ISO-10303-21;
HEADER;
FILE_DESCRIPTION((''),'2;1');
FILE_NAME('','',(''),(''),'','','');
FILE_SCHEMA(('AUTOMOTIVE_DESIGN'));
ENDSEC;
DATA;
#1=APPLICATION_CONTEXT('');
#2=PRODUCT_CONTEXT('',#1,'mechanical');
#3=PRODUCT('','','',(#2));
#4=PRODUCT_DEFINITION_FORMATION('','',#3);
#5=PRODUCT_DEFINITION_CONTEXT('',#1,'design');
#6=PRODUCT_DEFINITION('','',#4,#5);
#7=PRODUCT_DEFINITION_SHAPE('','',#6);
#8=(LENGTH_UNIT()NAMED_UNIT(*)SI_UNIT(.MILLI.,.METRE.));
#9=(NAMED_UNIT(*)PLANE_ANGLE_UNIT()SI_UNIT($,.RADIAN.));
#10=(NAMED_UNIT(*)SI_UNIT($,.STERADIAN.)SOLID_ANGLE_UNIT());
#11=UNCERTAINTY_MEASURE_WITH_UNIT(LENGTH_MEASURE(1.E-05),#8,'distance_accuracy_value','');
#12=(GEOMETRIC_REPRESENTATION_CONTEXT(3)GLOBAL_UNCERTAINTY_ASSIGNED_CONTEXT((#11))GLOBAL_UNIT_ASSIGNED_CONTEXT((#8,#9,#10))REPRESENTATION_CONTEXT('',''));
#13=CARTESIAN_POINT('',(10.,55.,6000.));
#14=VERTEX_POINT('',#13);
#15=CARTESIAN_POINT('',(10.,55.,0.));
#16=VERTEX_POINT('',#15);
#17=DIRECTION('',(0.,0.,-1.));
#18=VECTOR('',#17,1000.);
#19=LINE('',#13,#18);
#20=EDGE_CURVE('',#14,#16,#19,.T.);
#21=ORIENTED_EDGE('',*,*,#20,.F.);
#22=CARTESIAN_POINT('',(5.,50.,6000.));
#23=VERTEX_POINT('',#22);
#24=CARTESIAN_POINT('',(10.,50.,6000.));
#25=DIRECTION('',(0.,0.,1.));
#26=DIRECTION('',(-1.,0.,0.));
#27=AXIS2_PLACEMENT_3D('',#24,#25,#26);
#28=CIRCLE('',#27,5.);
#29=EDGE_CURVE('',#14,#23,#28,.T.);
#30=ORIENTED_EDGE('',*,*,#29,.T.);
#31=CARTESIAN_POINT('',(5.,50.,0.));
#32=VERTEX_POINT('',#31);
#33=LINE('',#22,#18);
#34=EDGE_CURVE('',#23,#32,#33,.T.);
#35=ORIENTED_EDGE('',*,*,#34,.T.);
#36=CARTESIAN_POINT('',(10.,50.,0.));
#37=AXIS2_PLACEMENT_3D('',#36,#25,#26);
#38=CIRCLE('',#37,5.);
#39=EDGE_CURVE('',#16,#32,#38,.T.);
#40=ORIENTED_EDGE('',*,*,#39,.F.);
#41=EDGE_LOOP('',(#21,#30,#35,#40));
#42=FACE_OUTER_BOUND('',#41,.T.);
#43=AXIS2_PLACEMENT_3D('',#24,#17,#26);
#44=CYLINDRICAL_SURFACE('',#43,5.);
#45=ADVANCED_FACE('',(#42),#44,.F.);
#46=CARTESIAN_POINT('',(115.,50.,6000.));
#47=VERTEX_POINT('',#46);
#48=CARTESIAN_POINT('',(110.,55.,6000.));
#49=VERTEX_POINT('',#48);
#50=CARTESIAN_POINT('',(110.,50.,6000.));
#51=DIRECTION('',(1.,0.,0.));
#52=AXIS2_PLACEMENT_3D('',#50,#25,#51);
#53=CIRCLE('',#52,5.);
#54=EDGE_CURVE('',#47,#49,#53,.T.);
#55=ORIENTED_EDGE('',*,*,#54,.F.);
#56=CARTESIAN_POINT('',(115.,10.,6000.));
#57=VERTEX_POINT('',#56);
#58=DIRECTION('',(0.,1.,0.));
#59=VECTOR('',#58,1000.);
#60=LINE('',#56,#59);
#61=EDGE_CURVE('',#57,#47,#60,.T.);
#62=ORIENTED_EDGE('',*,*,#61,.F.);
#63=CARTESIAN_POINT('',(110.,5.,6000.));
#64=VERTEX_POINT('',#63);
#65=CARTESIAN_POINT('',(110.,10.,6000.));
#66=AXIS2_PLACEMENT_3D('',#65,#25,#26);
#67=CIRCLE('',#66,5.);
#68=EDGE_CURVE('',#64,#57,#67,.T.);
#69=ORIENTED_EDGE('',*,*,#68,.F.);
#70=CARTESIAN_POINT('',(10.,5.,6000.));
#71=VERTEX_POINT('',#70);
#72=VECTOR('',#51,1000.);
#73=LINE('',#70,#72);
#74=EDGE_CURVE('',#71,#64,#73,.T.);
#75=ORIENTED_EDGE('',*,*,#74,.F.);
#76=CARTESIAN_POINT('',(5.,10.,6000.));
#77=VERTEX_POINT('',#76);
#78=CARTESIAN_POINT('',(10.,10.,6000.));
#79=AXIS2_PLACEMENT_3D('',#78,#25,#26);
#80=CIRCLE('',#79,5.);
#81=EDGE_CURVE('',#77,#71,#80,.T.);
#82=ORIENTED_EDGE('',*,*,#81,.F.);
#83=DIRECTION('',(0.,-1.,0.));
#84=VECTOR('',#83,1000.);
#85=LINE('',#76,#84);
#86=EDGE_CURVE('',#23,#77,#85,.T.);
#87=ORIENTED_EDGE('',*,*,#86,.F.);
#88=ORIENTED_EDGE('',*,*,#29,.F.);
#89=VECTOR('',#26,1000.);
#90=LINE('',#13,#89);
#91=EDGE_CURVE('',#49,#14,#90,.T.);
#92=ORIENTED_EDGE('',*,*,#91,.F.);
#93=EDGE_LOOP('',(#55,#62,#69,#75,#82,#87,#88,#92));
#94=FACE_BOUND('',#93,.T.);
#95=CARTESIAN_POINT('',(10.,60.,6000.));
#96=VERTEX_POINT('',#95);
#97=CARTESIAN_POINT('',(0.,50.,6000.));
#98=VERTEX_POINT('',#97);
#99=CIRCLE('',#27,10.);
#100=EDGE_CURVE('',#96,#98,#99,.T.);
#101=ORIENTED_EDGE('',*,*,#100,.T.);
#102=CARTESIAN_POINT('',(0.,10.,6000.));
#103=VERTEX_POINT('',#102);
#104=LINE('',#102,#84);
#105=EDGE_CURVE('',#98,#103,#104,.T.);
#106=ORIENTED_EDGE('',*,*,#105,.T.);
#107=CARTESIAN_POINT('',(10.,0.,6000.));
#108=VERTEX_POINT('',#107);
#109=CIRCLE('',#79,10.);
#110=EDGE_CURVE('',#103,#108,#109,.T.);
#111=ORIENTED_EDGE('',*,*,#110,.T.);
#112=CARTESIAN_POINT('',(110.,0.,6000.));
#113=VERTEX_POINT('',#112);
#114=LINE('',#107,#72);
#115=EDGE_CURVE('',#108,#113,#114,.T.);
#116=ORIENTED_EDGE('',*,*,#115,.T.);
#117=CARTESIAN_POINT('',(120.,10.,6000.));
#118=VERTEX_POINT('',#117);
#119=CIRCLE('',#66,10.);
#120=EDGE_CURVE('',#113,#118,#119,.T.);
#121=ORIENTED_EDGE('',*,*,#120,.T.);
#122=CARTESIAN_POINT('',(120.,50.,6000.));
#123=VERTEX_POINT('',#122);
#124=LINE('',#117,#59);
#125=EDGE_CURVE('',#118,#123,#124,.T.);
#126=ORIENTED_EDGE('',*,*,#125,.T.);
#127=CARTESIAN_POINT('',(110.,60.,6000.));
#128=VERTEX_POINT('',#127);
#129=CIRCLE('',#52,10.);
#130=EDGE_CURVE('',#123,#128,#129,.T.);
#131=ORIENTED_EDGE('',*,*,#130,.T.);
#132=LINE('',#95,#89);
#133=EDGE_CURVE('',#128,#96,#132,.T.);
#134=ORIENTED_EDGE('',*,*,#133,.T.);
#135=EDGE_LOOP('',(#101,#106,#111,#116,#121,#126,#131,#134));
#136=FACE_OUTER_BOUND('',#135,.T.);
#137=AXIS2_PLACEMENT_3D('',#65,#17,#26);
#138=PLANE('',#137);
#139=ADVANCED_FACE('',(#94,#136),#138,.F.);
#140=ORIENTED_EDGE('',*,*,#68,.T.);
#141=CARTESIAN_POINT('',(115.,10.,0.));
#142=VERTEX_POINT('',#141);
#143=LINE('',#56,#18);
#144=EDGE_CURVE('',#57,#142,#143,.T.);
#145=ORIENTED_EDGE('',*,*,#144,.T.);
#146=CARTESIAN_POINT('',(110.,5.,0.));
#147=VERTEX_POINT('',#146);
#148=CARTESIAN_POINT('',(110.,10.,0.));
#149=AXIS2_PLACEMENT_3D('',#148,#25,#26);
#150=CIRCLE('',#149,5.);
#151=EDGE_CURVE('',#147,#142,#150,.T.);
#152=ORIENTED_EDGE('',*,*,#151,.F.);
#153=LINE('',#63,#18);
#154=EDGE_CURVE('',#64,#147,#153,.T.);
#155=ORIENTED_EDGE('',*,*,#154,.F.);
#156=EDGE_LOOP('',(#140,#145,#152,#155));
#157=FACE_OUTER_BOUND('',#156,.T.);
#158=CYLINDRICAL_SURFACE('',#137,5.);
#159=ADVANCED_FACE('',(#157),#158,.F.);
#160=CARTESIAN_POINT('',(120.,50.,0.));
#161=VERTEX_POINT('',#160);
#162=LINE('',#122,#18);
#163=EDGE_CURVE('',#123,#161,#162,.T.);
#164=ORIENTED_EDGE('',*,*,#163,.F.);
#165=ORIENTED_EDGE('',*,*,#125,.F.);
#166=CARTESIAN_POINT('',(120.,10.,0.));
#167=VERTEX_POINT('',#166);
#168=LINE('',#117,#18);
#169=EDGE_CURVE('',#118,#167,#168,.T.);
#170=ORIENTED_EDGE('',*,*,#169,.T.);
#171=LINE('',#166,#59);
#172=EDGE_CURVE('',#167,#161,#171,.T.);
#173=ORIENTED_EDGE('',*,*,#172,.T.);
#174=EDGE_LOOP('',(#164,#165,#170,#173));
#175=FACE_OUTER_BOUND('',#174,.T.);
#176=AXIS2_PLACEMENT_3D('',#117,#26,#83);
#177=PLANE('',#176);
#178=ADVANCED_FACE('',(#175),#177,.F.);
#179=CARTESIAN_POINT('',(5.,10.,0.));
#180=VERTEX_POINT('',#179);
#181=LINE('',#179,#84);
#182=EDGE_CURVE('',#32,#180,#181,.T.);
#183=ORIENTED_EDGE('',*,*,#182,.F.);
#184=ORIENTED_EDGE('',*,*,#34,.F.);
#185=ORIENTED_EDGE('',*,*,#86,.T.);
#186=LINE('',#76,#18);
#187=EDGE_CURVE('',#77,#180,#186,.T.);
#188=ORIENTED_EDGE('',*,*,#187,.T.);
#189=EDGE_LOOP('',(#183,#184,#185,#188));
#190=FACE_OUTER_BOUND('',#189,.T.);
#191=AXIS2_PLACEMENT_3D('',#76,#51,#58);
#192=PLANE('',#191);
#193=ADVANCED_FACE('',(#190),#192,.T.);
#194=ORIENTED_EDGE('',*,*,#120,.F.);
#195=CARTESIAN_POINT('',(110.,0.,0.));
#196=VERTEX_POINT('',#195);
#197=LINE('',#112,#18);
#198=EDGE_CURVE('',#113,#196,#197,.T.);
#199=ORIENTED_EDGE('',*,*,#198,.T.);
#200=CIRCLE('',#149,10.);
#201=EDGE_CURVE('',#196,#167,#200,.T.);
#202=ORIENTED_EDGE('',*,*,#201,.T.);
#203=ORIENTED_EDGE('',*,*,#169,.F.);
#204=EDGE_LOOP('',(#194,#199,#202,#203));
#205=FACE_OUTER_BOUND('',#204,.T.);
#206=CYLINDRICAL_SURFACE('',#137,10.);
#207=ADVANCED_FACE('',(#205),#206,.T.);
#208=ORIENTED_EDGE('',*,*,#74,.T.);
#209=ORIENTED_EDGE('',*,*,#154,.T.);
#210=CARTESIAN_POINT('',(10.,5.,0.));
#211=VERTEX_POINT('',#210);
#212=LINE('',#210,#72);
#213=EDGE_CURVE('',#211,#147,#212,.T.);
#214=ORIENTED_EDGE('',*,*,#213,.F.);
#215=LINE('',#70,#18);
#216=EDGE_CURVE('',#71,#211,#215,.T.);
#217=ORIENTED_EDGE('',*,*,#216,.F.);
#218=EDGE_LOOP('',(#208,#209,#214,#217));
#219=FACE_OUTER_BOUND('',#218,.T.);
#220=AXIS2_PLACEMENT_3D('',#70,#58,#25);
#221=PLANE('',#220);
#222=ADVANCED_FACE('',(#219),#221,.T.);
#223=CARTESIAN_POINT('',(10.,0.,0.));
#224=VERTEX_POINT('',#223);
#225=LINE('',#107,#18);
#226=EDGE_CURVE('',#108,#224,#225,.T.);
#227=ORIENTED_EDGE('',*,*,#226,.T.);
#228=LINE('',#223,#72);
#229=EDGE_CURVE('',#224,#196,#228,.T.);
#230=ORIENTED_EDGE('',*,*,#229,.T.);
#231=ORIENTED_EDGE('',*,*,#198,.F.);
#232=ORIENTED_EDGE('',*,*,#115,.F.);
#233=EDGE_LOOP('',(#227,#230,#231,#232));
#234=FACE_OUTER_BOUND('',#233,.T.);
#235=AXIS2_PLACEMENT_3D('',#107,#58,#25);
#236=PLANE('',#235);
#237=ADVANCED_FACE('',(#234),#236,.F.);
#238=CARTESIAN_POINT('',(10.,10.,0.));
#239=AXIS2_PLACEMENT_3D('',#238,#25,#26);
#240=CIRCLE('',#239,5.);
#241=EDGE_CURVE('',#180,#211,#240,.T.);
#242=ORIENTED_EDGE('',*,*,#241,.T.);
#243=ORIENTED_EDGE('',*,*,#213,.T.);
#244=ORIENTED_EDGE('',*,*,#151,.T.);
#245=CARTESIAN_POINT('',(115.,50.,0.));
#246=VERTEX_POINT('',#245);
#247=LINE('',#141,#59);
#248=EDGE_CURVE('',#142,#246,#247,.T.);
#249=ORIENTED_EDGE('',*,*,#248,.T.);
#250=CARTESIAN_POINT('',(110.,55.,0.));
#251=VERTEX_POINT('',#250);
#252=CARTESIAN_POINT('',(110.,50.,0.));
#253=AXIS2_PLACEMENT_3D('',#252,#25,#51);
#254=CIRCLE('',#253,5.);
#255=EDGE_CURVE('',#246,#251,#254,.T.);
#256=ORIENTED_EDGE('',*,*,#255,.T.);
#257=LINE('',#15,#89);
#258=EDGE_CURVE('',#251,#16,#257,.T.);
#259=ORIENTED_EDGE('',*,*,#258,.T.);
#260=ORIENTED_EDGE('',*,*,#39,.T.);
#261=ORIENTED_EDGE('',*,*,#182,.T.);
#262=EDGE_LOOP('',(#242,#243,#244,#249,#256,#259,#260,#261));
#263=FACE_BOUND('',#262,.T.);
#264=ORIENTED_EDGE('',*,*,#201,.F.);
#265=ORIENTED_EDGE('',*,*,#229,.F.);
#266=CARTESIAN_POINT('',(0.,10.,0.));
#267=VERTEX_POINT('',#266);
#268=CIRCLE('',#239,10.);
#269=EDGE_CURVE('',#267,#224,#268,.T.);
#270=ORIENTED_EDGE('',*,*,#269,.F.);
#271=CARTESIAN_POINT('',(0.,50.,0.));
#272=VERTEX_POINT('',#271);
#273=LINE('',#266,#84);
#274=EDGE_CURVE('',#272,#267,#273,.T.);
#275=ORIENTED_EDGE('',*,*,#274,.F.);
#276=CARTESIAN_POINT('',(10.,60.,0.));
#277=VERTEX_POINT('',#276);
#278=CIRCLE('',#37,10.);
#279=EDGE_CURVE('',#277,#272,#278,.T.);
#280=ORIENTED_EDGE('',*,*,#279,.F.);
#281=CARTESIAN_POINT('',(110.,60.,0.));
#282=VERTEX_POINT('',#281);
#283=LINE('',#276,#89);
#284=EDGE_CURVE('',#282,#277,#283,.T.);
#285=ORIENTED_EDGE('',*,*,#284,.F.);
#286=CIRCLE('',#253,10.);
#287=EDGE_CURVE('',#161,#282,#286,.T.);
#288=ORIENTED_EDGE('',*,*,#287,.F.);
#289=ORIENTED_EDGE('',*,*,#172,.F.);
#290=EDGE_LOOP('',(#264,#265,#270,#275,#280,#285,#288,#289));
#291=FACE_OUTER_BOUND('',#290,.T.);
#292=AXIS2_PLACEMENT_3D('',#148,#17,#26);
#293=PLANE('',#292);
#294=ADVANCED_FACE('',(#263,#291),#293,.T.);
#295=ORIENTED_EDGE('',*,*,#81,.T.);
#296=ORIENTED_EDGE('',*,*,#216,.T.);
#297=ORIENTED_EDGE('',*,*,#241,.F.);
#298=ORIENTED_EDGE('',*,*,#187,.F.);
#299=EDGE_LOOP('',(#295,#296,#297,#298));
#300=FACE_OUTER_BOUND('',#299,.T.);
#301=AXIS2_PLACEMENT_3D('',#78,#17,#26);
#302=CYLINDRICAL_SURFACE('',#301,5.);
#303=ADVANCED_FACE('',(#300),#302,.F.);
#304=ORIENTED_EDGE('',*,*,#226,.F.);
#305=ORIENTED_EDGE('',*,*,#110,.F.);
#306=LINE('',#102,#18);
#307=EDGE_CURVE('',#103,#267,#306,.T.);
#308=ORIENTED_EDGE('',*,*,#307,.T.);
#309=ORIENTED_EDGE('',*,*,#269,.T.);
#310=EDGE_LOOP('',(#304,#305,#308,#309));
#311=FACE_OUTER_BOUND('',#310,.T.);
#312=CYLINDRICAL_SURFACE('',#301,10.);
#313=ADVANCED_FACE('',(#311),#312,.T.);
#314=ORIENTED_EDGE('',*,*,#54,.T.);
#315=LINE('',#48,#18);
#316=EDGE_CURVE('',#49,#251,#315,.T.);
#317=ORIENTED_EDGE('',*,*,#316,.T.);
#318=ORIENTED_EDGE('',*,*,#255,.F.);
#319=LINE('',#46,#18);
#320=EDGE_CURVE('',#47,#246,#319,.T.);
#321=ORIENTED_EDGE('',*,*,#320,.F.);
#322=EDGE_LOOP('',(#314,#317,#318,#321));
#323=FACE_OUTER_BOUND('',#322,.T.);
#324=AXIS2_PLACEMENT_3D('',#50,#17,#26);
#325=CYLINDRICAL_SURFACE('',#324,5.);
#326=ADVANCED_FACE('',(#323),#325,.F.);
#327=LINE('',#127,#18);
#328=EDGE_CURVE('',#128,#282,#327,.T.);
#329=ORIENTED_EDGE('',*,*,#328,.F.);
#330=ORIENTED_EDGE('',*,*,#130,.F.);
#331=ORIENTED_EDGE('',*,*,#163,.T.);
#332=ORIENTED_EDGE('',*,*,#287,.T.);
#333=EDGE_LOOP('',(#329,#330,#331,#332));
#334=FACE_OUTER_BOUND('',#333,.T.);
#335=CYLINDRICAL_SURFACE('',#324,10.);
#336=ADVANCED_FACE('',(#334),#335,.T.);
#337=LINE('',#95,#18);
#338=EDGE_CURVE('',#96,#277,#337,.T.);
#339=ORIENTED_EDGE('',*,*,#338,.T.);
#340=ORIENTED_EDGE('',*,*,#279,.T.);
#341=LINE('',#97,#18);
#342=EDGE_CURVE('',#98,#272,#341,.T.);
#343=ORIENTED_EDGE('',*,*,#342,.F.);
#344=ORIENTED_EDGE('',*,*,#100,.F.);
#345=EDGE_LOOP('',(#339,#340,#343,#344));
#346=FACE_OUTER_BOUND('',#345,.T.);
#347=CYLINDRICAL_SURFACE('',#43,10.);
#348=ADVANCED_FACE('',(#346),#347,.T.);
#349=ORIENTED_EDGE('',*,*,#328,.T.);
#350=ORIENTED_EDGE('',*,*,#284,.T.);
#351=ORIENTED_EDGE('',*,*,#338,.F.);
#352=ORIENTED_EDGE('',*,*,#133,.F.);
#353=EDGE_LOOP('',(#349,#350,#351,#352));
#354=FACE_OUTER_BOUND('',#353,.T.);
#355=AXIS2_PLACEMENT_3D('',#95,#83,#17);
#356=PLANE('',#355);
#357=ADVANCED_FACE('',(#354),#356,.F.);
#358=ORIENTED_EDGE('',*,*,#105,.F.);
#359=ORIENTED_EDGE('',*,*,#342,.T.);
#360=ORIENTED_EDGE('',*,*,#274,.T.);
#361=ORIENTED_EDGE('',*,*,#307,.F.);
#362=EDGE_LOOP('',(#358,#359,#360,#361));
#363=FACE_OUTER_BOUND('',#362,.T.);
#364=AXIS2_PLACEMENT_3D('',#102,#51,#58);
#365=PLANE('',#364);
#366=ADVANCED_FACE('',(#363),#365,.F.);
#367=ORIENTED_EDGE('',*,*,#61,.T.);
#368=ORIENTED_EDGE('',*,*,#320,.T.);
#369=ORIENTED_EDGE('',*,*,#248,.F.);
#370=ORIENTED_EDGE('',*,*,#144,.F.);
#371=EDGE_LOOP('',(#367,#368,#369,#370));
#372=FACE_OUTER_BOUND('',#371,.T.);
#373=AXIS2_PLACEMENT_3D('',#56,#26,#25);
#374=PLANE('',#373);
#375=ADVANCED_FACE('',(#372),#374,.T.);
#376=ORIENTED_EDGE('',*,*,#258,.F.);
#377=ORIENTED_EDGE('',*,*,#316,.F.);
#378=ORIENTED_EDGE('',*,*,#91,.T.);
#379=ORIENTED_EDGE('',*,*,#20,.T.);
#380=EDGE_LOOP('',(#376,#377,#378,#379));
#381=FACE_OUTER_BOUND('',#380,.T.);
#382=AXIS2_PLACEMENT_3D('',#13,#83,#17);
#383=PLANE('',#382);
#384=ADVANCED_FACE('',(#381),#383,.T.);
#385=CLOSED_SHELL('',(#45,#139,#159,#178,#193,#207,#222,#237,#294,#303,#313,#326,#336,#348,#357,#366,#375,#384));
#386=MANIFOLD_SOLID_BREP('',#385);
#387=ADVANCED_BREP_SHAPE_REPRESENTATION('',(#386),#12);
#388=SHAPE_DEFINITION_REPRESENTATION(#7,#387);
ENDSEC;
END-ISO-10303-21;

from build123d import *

# Parameters (mm, degrees)
BOSS_EXTRUDE1_DEPTH = 6000


with BuildPart() as part:
    # Sketch1 → Boss-Extrude1 (new body)
    with BuildSketch(Plane.XY):
        with BuildLine():
            Line((10, 0), (110, 0))
            ThreePointArc((110, 0), (117.071067812, 2.928932188), (120, 10))
            Line((120, 10), (120, 50))
            ThreePointArc((120, 50), (117.071067812, 57.071067812), (110, 60))
            Line((110, 60), (10, 60))
            ThreePointArc((10, 60), (2.928932188, 57.071067812), (0, 50))
            Line((0, 50), (0, 10))
            ThreePointArc((0, 10), (2.928932188, 2.928932188), (10, 0))
        make_face()
        with BuildLine():
            Line((10, 55), (110, 55))
            ThreePointArc((110, 55), (113.535533906, 53.535533906), (115, 50))
            Line((115, 50), (115, 10))
            ThreePointArc((115, 10), (113.535533906, 6.464466094), (110, 5))
            Line((110, 5), (10, 5))
            ThreePointArc((10, 5), (6.464466094, 6.464466094), (5, 10))
            Line((5, 10), (5, 50))
            ThreePointArc((5, 50), (6.464466094, 53.535533906), (10, 55))
        make_face(mode=Mode.SUBTRACT)
    extrude(amount=BOSS_EXTRUDE1_DEPTH)


solid = part.part
